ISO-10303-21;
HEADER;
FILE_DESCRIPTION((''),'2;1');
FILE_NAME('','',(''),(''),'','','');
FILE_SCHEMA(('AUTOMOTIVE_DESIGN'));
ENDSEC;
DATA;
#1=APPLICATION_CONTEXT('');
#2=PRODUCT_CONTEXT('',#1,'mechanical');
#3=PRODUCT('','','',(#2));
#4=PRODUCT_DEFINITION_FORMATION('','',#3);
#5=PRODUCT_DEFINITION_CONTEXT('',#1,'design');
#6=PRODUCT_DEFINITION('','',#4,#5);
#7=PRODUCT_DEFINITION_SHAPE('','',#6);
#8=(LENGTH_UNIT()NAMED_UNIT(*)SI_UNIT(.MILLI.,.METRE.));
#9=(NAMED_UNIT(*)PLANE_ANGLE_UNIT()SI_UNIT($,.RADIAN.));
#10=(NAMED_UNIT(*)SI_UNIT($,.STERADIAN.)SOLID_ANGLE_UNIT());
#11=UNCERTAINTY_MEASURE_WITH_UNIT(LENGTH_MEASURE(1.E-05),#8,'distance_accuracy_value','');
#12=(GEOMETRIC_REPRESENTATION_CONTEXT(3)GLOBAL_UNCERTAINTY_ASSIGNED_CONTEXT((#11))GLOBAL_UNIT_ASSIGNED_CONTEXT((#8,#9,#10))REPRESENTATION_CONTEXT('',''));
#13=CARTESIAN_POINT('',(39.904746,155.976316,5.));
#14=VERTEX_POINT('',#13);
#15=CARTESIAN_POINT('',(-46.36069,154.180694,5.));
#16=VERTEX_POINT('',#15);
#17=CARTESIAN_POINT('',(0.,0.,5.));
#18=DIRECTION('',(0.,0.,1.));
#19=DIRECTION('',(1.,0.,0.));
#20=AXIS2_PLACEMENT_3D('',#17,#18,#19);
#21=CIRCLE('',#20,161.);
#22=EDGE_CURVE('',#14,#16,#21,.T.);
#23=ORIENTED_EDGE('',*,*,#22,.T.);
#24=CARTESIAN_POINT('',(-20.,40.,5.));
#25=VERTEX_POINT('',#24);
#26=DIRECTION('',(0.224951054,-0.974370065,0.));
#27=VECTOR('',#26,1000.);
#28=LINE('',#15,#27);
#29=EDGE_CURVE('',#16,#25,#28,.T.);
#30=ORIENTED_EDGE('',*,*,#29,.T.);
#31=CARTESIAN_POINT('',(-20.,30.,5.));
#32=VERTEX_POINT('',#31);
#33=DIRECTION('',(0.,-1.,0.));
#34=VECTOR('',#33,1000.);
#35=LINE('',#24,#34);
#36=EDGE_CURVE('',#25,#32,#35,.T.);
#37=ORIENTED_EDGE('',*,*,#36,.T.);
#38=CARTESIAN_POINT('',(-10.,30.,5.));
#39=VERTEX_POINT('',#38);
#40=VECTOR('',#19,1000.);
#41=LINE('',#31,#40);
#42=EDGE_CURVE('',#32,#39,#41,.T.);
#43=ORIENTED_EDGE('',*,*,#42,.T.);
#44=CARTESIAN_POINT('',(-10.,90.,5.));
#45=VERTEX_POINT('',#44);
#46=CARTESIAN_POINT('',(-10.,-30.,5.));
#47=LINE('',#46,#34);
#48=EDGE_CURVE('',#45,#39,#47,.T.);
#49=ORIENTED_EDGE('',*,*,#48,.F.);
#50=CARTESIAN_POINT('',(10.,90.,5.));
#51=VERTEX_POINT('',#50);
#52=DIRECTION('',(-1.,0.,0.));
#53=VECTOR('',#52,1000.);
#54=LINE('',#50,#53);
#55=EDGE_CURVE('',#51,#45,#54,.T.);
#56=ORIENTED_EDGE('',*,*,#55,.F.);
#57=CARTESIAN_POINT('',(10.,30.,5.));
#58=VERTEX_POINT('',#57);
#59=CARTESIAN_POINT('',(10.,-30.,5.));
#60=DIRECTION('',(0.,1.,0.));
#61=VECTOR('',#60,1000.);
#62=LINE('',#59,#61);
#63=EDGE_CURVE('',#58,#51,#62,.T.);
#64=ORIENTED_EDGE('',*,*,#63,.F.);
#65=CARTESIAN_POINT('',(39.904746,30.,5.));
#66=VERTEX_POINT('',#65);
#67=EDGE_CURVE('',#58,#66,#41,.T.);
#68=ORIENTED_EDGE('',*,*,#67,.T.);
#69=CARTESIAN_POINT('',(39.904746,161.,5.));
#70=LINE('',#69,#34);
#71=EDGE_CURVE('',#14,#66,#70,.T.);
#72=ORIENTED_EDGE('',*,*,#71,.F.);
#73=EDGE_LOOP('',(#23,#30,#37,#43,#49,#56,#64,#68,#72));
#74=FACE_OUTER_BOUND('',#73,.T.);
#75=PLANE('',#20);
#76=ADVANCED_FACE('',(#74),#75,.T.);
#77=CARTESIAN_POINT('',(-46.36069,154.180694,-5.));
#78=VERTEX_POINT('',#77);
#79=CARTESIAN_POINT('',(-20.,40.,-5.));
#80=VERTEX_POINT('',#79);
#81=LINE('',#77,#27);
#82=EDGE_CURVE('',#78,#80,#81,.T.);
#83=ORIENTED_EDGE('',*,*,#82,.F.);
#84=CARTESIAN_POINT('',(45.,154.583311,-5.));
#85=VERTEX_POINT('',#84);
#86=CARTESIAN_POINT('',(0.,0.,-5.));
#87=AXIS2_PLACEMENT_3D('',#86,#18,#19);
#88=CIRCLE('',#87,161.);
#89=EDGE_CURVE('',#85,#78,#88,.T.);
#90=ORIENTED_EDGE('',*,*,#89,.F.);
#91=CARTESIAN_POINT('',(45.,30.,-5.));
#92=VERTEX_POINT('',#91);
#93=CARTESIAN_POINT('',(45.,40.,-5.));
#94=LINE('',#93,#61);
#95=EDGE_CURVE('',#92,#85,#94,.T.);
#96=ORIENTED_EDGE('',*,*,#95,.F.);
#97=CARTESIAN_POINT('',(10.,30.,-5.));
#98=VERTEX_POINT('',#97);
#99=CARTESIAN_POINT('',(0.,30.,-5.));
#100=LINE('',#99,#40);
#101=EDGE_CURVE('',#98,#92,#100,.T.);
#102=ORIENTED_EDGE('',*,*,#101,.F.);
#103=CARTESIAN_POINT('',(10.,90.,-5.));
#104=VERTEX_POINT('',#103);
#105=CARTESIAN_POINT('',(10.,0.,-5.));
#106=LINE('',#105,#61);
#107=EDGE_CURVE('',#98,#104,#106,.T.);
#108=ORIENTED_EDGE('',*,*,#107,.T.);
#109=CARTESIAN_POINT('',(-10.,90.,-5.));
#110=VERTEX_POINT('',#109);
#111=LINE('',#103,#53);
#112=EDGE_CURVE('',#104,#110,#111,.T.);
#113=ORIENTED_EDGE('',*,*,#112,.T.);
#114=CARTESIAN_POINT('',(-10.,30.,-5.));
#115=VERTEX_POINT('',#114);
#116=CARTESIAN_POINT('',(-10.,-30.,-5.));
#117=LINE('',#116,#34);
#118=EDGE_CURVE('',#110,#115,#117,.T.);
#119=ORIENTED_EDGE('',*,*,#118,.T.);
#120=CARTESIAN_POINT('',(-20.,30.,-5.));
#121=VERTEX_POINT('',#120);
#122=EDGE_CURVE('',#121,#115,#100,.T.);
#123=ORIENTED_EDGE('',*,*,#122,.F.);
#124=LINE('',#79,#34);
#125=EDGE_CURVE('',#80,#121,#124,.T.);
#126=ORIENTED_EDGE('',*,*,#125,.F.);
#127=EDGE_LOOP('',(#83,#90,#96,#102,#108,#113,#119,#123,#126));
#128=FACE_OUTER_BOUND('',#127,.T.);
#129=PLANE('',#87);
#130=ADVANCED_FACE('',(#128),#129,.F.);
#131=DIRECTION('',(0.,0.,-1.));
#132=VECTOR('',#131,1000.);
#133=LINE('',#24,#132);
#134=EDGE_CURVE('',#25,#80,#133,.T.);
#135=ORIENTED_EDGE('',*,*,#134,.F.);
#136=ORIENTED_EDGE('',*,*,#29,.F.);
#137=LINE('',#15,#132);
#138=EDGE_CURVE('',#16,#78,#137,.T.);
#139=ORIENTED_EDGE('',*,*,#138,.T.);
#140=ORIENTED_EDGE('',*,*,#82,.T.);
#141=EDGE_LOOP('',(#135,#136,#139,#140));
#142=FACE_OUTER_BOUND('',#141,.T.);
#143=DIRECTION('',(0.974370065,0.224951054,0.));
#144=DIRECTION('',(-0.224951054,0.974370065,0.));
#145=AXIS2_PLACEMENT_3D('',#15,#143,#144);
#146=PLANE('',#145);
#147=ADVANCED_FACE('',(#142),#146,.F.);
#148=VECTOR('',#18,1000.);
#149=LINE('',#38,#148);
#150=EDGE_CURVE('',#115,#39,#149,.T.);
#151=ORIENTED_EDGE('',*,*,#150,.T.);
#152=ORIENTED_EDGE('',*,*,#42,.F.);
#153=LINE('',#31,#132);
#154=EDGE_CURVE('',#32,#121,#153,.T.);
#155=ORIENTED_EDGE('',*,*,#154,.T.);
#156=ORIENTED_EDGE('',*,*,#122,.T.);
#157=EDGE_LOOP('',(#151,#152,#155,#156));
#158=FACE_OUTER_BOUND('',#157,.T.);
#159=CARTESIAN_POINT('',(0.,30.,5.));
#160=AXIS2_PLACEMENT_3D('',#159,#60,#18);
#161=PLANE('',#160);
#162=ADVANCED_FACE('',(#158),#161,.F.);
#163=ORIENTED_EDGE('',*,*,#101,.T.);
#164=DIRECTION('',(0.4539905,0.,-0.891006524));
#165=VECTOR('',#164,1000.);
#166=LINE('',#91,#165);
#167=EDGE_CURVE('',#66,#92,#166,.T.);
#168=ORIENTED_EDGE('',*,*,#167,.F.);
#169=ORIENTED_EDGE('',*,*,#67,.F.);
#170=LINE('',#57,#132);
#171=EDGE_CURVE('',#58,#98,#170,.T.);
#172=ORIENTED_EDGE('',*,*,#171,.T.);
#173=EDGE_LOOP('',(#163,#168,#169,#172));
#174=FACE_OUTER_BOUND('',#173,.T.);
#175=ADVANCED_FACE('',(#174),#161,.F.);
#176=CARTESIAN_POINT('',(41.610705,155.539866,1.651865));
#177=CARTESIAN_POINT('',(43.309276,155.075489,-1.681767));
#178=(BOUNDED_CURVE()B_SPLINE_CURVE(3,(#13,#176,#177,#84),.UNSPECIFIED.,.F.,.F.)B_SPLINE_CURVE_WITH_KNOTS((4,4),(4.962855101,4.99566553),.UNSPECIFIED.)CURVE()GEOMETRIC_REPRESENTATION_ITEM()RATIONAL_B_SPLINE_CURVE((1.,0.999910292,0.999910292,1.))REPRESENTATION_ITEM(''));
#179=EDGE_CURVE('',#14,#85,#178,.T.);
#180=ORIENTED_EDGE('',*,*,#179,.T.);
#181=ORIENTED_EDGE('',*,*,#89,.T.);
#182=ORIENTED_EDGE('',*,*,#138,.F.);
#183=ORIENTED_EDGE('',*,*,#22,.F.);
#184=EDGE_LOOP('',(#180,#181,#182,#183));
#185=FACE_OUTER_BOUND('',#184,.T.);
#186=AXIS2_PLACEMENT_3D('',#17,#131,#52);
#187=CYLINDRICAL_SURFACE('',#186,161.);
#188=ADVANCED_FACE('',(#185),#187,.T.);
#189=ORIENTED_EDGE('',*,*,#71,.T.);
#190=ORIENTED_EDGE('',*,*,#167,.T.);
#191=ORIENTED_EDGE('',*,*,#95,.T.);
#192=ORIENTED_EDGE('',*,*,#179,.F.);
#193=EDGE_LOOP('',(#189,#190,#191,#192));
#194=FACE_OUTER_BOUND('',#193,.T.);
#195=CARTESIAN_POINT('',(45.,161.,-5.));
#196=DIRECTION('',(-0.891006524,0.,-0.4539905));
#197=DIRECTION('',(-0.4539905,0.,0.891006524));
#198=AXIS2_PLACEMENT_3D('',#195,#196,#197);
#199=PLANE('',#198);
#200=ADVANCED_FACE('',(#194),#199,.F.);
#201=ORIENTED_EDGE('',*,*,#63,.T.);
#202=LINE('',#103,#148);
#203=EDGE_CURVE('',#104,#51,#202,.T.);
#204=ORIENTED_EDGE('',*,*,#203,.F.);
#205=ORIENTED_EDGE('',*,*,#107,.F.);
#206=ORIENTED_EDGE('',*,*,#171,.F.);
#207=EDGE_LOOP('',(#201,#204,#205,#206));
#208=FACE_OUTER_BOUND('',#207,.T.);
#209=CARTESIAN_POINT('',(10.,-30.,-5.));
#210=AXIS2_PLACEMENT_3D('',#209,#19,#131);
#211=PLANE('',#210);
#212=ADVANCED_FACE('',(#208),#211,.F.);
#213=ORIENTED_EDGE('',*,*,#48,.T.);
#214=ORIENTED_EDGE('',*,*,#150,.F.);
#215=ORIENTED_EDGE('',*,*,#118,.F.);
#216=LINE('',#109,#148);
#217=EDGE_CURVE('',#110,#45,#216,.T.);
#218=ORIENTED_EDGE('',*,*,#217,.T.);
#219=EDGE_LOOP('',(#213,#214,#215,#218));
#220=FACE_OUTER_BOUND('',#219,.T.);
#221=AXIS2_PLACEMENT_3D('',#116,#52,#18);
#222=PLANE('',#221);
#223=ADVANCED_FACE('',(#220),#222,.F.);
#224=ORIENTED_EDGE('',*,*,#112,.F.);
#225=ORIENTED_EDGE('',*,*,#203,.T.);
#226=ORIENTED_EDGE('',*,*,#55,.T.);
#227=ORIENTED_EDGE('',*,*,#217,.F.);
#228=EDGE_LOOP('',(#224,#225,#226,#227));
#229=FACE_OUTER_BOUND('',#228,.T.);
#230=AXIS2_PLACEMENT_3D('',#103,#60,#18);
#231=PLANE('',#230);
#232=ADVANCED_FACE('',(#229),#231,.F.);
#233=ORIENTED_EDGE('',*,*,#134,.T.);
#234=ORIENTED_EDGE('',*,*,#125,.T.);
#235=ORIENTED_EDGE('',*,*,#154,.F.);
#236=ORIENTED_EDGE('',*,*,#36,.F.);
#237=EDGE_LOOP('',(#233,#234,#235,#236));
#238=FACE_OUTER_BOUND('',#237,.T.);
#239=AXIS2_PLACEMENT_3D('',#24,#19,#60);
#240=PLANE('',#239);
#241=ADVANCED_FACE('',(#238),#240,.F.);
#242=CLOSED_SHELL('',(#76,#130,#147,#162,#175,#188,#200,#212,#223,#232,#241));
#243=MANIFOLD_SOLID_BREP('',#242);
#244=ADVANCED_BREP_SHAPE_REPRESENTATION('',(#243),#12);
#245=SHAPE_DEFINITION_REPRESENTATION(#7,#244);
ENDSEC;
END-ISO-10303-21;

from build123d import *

# Parameters (mm, degrees)
BOSS_EXTRUDE1_DEPTH = 5
SKETCH2_W           = 20
SKETCH2_H           = 120
CUT_EXTRUDE1_DEPTH  = 10
CUT_EXTRUDE2_DEPTH  = 140.051478249


with BuildPart() as part:
    # Sketch1 → Boss-Extrude1 (new, symmetric)
    with BuildSketch(Plane.XY):
        with BuildLine():
            Line((-46.360690281, 154.180693982), (-20, 40))
            Line((-20, 40), (-20, 30))
            Line((-20, 30), (0, 30))
            Line((0, 30), (45, 30))
            Line((45, 30), (45, 40))
            Line((45, 40), (45, 154.583310872))
            ThreePointArc((45, 154.583310872), (-0.709503066, 160.998436655), (-46.360690281, 154.180693982))
        make_face()
    extrude(amount=BOSS_EXTRUDE1_DEPTH, both=True)

    # Sketch2 → Cut-Extrude1 (cut)
    with BuildSketch(Plane.XY.offset(5)):
        with Locations((0, 30)):
            Rectangle(SKETCH2_W, SKETCH2_H)
    extrude(amount=-CUT_EXTRUDE1_DEPTH, mode=Mode.SUBTRACT)

    # Sketch3 → Cut-Extrude2 (cut, through all)
    with BuildSketch(Plane.XZ.offset(-30)):
        Polygon((45, -5), (39.904745505, 5), (45, 5), align=None)
    extrude(amount=-CUT_EXTRUDE2_DEPTH, mode=Mode.SUBTRACT)


solid = part.part
